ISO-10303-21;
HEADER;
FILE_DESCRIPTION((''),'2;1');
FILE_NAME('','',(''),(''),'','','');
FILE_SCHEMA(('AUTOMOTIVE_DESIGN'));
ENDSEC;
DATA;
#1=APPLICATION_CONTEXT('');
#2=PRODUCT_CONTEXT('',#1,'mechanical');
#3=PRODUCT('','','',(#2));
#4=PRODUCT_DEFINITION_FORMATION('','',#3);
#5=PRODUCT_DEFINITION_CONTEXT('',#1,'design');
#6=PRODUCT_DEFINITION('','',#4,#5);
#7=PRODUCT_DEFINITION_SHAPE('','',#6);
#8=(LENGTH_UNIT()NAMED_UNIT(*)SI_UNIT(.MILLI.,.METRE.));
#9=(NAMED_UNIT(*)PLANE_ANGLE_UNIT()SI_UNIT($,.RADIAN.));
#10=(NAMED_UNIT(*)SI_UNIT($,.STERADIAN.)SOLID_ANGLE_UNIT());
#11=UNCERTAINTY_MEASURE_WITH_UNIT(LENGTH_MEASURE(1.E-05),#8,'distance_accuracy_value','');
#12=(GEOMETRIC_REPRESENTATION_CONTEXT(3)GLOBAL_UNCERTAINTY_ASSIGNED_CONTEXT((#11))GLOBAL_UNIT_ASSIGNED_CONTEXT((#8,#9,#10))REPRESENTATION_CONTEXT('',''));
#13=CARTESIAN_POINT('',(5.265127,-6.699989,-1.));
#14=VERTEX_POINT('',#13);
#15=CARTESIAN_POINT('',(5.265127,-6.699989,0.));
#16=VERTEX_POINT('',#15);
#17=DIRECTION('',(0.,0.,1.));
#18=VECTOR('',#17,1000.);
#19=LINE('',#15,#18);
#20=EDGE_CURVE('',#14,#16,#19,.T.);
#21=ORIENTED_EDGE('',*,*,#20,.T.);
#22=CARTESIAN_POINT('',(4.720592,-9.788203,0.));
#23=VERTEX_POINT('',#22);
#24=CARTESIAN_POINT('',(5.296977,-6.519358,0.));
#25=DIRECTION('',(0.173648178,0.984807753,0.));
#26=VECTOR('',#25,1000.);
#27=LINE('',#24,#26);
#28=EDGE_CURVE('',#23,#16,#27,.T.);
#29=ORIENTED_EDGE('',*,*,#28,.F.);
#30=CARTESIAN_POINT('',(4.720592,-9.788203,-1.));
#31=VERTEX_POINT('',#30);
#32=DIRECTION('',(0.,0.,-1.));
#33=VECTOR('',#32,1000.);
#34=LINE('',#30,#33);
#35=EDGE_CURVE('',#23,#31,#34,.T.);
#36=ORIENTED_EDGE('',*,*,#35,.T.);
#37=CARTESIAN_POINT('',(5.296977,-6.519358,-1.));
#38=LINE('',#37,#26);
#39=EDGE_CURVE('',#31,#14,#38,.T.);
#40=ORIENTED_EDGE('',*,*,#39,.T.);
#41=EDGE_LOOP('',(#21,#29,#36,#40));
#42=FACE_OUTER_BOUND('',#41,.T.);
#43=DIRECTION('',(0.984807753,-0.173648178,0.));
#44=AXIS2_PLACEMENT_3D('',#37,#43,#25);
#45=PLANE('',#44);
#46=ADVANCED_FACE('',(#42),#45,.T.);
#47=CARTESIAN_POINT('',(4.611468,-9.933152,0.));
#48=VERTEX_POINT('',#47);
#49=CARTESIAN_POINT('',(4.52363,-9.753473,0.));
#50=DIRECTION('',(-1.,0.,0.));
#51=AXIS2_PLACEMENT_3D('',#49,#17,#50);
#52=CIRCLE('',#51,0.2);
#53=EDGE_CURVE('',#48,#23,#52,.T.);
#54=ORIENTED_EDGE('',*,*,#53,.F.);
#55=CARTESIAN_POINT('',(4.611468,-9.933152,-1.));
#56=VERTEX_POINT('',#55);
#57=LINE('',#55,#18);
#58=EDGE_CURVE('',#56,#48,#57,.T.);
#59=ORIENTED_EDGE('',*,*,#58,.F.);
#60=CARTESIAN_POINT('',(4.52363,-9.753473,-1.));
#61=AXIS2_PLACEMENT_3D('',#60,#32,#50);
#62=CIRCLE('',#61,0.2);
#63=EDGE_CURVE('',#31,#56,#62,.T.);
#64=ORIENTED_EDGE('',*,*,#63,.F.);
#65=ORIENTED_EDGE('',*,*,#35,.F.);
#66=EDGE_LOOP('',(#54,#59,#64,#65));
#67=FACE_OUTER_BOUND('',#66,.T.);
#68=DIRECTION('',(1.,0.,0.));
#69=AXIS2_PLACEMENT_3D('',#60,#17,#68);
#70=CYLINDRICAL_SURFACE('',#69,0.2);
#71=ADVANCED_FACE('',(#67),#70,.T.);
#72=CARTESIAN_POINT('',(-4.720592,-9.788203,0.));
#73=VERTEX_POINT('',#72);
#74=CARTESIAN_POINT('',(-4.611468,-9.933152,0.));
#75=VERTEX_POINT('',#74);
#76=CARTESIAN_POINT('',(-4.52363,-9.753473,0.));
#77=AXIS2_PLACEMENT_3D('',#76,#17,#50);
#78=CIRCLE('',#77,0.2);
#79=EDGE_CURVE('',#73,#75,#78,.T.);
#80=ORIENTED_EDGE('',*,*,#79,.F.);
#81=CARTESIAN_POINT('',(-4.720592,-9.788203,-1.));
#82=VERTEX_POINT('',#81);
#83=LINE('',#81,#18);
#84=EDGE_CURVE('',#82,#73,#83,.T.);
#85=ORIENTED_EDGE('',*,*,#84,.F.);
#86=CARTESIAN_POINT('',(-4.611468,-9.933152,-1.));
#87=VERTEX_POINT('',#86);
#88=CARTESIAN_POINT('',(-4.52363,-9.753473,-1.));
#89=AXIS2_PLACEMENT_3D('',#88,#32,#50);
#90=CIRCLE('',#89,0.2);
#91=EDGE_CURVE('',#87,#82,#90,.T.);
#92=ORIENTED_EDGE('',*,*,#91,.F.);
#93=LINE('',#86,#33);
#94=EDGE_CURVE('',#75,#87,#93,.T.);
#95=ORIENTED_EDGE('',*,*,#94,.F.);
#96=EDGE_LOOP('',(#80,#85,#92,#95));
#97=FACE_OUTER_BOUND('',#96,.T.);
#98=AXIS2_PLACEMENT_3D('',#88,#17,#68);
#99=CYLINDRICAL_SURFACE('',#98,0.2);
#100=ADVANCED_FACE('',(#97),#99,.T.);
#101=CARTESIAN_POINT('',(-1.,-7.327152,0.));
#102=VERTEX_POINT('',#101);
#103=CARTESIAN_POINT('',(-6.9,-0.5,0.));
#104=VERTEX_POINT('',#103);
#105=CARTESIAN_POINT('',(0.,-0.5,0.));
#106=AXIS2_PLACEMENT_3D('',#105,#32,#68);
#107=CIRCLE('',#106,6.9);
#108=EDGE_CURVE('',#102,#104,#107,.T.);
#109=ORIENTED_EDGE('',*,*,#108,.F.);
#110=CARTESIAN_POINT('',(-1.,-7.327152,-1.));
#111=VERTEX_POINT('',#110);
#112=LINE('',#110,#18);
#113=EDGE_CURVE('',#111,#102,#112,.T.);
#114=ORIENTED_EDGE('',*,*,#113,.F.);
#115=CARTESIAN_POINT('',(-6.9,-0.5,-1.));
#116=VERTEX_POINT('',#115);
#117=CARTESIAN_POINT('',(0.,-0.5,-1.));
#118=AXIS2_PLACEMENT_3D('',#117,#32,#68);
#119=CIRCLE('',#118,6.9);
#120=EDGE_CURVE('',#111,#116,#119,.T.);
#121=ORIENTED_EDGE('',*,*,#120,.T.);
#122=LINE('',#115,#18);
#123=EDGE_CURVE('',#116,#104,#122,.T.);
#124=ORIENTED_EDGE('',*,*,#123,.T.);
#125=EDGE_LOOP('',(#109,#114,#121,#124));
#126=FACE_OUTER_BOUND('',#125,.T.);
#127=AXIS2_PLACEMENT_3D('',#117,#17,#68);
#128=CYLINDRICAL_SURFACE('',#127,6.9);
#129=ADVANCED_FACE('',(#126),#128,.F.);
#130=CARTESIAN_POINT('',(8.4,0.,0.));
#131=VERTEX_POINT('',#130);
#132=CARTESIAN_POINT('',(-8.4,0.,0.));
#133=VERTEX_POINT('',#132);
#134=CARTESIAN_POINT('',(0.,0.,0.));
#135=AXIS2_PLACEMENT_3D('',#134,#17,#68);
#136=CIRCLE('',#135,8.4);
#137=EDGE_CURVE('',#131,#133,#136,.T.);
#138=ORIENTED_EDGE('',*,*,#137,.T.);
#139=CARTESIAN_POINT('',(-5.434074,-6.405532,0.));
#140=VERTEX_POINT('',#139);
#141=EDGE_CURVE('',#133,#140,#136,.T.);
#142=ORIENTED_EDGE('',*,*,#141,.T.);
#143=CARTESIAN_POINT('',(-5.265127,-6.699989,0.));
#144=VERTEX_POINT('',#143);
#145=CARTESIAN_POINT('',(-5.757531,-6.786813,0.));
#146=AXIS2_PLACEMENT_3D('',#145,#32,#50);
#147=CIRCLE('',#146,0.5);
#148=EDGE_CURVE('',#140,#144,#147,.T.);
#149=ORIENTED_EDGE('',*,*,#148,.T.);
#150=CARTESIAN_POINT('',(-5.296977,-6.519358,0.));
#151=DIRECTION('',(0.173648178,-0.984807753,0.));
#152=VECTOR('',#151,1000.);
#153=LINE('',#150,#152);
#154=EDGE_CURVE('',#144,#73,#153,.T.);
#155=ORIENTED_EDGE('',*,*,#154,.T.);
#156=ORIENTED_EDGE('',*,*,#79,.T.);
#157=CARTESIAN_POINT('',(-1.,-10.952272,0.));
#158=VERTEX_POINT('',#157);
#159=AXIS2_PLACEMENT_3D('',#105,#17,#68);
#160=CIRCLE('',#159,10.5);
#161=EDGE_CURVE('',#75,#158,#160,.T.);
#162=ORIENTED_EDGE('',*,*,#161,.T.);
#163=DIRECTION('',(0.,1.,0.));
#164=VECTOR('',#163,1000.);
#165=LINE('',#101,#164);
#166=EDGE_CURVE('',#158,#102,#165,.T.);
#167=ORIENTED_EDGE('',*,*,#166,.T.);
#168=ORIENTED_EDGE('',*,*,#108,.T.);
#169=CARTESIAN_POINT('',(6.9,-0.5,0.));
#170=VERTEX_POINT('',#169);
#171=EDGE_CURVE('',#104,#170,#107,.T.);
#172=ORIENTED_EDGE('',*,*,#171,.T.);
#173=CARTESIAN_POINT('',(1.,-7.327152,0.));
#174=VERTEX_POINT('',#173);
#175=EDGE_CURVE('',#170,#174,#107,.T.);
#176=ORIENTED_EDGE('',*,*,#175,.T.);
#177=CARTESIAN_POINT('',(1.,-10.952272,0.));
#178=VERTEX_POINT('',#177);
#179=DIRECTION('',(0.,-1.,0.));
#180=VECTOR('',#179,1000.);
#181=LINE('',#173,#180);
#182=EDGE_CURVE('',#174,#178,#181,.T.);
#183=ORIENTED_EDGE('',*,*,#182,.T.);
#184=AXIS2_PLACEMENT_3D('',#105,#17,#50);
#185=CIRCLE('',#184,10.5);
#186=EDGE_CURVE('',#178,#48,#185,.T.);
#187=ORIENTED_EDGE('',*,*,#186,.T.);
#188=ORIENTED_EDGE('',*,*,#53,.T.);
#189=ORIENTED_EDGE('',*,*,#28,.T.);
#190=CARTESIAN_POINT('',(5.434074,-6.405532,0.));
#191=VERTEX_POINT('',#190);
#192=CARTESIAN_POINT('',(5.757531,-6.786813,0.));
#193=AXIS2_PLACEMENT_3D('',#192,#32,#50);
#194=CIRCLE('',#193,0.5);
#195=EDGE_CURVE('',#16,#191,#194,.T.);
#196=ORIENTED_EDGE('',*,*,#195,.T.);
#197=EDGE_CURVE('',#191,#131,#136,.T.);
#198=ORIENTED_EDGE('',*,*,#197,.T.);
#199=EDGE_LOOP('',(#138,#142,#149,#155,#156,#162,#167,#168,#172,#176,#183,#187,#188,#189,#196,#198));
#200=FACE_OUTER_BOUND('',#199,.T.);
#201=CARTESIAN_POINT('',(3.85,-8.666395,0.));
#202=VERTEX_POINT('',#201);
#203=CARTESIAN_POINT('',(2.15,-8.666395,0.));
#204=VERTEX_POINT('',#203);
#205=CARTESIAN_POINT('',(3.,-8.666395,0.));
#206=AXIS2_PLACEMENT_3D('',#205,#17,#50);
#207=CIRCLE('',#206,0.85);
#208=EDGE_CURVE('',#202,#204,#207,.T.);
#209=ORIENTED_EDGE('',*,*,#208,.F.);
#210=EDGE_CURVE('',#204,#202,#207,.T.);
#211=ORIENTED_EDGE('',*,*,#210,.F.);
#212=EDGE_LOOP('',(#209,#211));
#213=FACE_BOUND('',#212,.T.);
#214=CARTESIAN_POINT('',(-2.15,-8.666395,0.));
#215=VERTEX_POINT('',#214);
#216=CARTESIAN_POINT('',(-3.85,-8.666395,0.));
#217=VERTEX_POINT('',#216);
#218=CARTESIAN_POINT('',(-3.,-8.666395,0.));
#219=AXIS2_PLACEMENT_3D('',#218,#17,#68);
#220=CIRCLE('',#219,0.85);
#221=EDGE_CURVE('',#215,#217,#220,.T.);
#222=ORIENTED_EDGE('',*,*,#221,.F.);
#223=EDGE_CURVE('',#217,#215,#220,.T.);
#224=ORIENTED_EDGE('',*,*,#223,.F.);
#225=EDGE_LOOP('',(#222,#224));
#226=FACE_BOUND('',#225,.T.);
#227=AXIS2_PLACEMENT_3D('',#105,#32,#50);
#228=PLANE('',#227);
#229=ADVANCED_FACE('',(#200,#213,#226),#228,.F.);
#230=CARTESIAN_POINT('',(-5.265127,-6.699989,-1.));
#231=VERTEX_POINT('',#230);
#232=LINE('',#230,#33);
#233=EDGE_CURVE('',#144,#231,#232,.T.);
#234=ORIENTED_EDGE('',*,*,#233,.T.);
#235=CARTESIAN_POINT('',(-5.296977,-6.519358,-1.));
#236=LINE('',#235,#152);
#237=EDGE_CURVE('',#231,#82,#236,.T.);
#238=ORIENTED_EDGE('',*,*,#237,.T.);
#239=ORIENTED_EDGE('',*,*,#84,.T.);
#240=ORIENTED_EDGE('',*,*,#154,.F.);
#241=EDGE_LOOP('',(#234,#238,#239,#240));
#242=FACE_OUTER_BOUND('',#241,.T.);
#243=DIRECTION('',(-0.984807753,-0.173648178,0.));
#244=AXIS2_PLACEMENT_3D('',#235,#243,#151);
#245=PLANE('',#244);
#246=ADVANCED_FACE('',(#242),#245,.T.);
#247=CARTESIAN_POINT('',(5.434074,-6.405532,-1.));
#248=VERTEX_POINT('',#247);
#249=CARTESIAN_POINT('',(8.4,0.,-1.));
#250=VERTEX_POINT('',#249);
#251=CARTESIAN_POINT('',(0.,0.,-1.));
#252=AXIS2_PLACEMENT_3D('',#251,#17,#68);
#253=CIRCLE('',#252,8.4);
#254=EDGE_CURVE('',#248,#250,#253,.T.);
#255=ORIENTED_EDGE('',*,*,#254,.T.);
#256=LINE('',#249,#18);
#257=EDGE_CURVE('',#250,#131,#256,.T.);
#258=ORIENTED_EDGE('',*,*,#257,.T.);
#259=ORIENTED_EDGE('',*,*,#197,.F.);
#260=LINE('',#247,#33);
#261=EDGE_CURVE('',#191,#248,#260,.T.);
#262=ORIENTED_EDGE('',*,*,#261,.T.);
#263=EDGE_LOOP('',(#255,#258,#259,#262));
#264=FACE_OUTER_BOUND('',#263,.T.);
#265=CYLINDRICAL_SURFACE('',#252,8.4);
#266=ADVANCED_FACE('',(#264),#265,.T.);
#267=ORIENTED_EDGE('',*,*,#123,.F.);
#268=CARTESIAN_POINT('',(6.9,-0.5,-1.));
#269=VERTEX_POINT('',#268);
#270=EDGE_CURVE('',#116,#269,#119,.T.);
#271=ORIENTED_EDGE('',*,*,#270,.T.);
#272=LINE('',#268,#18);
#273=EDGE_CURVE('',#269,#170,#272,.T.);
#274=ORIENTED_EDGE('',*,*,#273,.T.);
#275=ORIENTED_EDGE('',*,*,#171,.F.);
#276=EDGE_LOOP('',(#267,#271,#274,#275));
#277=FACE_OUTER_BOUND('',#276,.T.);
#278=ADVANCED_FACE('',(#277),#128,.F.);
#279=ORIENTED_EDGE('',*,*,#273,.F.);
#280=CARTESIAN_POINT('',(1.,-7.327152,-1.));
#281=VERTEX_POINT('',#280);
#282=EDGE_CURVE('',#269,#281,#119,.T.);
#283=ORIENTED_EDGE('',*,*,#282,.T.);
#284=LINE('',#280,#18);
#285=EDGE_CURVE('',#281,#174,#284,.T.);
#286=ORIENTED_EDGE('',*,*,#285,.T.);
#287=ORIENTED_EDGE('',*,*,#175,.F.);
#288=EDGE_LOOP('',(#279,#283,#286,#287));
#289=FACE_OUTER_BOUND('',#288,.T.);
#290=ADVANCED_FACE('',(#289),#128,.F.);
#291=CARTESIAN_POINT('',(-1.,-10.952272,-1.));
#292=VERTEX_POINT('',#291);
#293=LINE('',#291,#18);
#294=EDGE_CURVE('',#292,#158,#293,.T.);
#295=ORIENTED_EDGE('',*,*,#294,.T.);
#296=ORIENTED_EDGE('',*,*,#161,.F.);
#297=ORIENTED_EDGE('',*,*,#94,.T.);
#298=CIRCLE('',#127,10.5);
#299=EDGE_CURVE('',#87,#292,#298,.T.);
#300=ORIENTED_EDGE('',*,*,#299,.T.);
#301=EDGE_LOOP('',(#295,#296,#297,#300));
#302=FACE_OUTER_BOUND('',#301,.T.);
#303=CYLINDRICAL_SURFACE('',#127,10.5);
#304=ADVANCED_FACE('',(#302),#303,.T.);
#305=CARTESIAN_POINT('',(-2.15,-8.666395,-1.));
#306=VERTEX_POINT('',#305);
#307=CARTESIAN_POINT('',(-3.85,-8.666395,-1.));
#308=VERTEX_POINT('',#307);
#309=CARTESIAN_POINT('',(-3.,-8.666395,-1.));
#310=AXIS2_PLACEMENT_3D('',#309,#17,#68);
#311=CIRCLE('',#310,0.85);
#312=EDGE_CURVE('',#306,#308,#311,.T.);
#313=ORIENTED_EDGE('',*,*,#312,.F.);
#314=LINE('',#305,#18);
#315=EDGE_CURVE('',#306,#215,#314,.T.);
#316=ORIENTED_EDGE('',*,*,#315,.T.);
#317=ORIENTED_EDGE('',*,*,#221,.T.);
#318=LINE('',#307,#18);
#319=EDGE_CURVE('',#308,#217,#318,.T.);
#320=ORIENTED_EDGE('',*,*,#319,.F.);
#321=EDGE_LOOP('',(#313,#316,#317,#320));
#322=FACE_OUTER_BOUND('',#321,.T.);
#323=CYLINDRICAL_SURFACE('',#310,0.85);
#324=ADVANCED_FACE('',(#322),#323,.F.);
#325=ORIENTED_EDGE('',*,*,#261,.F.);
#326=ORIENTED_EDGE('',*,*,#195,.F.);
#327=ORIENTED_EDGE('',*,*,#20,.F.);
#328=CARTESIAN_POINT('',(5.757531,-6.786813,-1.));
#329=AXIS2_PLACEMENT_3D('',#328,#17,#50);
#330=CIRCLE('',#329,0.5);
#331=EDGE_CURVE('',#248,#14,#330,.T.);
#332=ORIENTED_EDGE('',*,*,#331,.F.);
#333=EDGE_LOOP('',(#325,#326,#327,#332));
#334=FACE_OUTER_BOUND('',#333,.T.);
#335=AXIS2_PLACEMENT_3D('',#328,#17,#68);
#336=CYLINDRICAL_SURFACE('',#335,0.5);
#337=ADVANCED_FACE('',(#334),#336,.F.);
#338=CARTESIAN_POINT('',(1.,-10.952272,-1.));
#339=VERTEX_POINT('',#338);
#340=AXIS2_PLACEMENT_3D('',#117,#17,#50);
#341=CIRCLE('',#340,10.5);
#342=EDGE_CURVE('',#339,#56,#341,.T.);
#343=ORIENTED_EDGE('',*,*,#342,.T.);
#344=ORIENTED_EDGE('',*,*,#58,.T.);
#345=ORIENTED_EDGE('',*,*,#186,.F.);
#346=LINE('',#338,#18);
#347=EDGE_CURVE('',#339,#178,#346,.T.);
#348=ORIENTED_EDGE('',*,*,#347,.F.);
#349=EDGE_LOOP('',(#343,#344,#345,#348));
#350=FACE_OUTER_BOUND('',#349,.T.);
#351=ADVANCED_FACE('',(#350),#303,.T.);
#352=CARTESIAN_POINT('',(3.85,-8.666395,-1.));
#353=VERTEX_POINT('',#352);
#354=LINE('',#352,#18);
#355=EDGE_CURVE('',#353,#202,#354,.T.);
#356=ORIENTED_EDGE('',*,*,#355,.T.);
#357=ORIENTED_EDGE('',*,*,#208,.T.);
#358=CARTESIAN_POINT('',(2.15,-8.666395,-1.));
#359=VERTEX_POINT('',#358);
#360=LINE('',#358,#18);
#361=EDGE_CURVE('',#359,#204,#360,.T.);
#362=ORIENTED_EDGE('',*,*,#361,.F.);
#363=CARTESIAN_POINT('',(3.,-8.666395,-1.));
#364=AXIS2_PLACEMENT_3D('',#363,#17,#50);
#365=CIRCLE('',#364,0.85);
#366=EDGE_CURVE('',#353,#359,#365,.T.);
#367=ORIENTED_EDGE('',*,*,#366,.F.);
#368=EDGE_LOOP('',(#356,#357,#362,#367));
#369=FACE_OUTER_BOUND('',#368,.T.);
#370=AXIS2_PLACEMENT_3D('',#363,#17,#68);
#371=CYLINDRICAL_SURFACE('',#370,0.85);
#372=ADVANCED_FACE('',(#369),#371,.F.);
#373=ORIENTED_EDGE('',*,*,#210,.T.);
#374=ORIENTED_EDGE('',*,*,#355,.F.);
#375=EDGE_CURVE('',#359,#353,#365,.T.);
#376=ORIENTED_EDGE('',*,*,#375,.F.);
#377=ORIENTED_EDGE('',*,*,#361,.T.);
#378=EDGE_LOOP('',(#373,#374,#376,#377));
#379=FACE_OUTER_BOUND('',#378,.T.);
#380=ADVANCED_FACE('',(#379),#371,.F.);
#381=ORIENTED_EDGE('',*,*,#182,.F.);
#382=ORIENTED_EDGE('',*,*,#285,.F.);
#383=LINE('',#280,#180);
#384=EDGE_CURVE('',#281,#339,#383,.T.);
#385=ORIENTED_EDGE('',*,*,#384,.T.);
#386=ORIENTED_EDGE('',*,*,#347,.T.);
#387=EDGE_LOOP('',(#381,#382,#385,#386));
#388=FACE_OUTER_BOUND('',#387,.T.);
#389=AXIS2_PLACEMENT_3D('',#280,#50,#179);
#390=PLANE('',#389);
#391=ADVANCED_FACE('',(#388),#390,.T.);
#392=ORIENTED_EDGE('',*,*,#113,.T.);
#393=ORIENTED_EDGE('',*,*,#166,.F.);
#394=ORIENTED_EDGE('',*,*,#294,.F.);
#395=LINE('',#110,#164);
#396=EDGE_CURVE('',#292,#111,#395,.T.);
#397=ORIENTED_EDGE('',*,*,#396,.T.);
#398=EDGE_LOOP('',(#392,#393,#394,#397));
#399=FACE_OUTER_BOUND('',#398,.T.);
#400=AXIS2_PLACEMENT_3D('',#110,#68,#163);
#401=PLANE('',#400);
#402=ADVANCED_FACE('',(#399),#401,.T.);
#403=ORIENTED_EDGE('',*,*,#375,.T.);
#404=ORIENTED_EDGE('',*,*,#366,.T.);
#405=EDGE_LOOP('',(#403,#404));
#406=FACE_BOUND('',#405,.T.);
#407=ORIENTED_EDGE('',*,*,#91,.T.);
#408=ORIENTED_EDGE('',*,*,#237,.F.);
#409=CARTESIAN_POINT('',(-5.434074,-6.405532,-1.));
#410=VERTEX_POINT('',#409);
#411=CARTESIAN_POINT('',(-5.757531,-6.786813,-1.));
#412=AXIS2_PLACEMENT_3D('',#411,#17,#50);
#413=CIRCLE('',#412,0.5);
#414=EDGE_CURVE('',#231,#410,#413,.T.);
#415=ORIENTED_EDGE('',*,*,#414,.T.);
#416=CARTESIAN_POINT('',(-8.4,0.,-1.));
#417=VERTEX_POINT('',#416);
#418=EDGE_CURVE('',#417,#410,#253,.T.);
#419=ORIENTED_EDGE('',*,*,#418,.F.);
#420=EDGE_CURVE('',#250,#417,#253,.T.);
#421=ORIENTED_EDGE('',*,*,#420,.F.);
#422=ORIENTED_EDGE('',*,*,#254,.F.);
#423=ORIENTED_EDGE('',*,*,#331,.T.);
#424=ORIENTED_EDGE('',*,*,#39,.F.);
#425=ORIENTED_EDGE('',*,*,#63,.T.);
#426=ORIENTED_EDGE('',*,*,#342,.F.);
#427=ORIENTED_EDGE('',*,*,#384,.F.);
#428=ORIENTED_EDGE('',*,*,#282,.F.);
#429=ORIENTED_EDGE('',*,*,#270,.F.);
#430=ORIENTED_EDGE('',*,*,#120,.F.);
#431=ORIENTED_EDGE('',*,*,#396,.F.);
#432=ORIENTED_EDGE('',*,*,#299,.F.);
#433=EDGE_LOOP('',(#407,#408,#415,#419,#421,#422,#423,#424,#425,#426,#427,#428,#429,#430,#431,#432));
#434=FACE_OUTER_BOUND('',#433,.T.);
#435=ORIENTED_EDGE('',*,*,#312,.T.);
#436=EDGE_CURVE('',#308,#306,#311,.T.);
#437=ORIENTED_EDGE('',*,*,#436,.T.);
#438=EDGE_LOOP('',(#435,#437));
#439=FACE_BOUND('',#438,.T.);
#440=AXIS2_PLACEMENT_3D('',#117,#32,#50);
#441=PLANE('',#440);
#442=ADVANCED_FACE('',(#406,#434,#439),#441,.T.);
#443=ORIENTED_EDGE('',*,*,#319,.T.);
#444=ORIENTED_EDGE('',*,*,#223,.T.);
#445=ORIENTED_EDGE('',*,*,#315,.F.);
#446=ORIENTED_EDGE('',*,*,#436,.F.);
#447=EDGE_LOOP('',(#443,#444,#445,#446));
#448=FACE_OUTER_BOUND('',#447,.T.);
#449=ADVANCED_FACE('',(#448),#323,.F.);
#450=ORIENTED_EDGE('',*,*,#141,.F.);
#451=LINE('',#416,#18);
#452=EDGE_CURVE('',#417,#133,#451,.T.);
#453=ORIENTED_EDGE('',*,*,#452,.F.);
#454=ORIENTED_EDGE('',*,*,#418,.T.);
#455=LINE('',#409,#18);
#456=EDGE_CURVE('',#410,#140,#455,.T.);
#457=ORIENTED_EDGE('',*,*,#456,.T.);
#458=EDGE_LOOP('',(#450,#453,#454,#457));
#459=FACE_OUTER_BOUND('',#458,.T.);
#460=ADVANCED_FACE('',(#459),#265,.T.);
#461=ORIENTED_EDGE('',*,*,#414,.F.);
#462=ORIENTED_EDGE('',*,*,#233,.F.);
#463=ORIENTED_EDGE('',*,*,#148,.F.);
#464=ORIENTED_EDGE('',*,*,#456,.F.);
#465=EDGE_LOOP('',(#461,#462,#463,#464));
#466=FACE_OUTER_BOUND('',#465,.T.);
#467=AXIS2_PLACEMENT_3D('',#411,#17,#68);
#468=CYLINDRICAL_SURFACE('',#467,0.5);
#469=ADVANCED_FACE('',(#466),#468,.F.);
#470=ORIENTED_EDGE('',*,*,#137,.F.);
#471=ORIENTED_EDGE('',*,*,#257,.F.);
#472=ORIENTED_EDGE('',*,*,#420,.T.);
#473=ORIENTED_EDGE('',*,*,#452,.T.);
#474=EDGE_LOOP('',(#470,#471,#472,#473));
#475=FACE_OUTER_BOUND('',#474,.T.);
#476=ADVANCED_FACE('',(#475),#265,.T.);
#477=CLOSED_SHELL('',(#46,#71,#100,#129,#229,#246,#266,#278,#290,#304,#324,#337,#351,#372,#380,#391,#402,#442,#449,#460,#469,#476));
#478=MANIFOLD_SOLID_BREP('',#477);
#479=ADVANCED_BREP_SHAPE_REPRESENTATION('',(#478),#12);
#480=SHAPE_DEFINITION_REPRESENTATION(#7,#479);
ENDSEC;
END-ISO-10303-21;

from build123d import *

# Parameters (mm, degrees)
SKETCH1_R  = 0.85
BODY_DEPTH = 1
FILLET1_R  = 0.2
FILLET2_R  = 0.5


with BuildPart() as part:
    # Sketch1 → Body (new body)
    with BuildSketch(Plane.XY):
        with BuildLine():
            Line((-1, -7.327151675), (-1, -10.95227248))
            ThreePointArc((-1, -10.95227248), (-2.900753364, -10.591364126), (-4.703022713, -9.887841997))
            Line((-4.703022713, -9.887841997), (-5.296977287, -6.519358222))
            ThreePointArc((-5.296977287, -6.519358222), (0, 8.4), (5.296977287, -6.519358222))
            Line((5.296977287, -6.519358222), (4.703022713, -9.887841997))
            ThreePointArc((4.703022713, -9.887841997), (2.900753364, -10.591364126), (1, -10.95227248))
            Line((1, -10.95227248), (1, -7.327151675))
            ThreePointArc((1, -7.327151675), (0, 6.4), (-1, -7.327151675))
        make_face()
        with Locations(Location((3, -8.666394553, 0), (0, 0, 180))):
            Circle(SKETCH1_R, mode=Mode.SUBTRACT)
        with Locations((-3, -8.666394553)):
            Circle(SKETCH1_R, mode=Mode.SUBTRACT)
    extrude(amount=-BODY_DEPTH)

    # Fillet1
    fillet1_edges = [part.edges().sort_by_distance(p)[0] for p in [
        (-4.703022713, -9.887841997, -0.5),
        (4.703022713, -9.887841997, -0.5),
    ]]
    fillet(fillet1_edges, radius=FILLET1_R)

    # Fillet2
    fillet2_edges = [part.edges().sort_by_distance(p)[0] for p in [
        (-5.296977287, -6.519358222, -0.5),
        (5.296977287, -6.519358222, -0.5),
    ]]
    fillet(fillet2_edges, radius=FILLET2_R)


solid = part.part
